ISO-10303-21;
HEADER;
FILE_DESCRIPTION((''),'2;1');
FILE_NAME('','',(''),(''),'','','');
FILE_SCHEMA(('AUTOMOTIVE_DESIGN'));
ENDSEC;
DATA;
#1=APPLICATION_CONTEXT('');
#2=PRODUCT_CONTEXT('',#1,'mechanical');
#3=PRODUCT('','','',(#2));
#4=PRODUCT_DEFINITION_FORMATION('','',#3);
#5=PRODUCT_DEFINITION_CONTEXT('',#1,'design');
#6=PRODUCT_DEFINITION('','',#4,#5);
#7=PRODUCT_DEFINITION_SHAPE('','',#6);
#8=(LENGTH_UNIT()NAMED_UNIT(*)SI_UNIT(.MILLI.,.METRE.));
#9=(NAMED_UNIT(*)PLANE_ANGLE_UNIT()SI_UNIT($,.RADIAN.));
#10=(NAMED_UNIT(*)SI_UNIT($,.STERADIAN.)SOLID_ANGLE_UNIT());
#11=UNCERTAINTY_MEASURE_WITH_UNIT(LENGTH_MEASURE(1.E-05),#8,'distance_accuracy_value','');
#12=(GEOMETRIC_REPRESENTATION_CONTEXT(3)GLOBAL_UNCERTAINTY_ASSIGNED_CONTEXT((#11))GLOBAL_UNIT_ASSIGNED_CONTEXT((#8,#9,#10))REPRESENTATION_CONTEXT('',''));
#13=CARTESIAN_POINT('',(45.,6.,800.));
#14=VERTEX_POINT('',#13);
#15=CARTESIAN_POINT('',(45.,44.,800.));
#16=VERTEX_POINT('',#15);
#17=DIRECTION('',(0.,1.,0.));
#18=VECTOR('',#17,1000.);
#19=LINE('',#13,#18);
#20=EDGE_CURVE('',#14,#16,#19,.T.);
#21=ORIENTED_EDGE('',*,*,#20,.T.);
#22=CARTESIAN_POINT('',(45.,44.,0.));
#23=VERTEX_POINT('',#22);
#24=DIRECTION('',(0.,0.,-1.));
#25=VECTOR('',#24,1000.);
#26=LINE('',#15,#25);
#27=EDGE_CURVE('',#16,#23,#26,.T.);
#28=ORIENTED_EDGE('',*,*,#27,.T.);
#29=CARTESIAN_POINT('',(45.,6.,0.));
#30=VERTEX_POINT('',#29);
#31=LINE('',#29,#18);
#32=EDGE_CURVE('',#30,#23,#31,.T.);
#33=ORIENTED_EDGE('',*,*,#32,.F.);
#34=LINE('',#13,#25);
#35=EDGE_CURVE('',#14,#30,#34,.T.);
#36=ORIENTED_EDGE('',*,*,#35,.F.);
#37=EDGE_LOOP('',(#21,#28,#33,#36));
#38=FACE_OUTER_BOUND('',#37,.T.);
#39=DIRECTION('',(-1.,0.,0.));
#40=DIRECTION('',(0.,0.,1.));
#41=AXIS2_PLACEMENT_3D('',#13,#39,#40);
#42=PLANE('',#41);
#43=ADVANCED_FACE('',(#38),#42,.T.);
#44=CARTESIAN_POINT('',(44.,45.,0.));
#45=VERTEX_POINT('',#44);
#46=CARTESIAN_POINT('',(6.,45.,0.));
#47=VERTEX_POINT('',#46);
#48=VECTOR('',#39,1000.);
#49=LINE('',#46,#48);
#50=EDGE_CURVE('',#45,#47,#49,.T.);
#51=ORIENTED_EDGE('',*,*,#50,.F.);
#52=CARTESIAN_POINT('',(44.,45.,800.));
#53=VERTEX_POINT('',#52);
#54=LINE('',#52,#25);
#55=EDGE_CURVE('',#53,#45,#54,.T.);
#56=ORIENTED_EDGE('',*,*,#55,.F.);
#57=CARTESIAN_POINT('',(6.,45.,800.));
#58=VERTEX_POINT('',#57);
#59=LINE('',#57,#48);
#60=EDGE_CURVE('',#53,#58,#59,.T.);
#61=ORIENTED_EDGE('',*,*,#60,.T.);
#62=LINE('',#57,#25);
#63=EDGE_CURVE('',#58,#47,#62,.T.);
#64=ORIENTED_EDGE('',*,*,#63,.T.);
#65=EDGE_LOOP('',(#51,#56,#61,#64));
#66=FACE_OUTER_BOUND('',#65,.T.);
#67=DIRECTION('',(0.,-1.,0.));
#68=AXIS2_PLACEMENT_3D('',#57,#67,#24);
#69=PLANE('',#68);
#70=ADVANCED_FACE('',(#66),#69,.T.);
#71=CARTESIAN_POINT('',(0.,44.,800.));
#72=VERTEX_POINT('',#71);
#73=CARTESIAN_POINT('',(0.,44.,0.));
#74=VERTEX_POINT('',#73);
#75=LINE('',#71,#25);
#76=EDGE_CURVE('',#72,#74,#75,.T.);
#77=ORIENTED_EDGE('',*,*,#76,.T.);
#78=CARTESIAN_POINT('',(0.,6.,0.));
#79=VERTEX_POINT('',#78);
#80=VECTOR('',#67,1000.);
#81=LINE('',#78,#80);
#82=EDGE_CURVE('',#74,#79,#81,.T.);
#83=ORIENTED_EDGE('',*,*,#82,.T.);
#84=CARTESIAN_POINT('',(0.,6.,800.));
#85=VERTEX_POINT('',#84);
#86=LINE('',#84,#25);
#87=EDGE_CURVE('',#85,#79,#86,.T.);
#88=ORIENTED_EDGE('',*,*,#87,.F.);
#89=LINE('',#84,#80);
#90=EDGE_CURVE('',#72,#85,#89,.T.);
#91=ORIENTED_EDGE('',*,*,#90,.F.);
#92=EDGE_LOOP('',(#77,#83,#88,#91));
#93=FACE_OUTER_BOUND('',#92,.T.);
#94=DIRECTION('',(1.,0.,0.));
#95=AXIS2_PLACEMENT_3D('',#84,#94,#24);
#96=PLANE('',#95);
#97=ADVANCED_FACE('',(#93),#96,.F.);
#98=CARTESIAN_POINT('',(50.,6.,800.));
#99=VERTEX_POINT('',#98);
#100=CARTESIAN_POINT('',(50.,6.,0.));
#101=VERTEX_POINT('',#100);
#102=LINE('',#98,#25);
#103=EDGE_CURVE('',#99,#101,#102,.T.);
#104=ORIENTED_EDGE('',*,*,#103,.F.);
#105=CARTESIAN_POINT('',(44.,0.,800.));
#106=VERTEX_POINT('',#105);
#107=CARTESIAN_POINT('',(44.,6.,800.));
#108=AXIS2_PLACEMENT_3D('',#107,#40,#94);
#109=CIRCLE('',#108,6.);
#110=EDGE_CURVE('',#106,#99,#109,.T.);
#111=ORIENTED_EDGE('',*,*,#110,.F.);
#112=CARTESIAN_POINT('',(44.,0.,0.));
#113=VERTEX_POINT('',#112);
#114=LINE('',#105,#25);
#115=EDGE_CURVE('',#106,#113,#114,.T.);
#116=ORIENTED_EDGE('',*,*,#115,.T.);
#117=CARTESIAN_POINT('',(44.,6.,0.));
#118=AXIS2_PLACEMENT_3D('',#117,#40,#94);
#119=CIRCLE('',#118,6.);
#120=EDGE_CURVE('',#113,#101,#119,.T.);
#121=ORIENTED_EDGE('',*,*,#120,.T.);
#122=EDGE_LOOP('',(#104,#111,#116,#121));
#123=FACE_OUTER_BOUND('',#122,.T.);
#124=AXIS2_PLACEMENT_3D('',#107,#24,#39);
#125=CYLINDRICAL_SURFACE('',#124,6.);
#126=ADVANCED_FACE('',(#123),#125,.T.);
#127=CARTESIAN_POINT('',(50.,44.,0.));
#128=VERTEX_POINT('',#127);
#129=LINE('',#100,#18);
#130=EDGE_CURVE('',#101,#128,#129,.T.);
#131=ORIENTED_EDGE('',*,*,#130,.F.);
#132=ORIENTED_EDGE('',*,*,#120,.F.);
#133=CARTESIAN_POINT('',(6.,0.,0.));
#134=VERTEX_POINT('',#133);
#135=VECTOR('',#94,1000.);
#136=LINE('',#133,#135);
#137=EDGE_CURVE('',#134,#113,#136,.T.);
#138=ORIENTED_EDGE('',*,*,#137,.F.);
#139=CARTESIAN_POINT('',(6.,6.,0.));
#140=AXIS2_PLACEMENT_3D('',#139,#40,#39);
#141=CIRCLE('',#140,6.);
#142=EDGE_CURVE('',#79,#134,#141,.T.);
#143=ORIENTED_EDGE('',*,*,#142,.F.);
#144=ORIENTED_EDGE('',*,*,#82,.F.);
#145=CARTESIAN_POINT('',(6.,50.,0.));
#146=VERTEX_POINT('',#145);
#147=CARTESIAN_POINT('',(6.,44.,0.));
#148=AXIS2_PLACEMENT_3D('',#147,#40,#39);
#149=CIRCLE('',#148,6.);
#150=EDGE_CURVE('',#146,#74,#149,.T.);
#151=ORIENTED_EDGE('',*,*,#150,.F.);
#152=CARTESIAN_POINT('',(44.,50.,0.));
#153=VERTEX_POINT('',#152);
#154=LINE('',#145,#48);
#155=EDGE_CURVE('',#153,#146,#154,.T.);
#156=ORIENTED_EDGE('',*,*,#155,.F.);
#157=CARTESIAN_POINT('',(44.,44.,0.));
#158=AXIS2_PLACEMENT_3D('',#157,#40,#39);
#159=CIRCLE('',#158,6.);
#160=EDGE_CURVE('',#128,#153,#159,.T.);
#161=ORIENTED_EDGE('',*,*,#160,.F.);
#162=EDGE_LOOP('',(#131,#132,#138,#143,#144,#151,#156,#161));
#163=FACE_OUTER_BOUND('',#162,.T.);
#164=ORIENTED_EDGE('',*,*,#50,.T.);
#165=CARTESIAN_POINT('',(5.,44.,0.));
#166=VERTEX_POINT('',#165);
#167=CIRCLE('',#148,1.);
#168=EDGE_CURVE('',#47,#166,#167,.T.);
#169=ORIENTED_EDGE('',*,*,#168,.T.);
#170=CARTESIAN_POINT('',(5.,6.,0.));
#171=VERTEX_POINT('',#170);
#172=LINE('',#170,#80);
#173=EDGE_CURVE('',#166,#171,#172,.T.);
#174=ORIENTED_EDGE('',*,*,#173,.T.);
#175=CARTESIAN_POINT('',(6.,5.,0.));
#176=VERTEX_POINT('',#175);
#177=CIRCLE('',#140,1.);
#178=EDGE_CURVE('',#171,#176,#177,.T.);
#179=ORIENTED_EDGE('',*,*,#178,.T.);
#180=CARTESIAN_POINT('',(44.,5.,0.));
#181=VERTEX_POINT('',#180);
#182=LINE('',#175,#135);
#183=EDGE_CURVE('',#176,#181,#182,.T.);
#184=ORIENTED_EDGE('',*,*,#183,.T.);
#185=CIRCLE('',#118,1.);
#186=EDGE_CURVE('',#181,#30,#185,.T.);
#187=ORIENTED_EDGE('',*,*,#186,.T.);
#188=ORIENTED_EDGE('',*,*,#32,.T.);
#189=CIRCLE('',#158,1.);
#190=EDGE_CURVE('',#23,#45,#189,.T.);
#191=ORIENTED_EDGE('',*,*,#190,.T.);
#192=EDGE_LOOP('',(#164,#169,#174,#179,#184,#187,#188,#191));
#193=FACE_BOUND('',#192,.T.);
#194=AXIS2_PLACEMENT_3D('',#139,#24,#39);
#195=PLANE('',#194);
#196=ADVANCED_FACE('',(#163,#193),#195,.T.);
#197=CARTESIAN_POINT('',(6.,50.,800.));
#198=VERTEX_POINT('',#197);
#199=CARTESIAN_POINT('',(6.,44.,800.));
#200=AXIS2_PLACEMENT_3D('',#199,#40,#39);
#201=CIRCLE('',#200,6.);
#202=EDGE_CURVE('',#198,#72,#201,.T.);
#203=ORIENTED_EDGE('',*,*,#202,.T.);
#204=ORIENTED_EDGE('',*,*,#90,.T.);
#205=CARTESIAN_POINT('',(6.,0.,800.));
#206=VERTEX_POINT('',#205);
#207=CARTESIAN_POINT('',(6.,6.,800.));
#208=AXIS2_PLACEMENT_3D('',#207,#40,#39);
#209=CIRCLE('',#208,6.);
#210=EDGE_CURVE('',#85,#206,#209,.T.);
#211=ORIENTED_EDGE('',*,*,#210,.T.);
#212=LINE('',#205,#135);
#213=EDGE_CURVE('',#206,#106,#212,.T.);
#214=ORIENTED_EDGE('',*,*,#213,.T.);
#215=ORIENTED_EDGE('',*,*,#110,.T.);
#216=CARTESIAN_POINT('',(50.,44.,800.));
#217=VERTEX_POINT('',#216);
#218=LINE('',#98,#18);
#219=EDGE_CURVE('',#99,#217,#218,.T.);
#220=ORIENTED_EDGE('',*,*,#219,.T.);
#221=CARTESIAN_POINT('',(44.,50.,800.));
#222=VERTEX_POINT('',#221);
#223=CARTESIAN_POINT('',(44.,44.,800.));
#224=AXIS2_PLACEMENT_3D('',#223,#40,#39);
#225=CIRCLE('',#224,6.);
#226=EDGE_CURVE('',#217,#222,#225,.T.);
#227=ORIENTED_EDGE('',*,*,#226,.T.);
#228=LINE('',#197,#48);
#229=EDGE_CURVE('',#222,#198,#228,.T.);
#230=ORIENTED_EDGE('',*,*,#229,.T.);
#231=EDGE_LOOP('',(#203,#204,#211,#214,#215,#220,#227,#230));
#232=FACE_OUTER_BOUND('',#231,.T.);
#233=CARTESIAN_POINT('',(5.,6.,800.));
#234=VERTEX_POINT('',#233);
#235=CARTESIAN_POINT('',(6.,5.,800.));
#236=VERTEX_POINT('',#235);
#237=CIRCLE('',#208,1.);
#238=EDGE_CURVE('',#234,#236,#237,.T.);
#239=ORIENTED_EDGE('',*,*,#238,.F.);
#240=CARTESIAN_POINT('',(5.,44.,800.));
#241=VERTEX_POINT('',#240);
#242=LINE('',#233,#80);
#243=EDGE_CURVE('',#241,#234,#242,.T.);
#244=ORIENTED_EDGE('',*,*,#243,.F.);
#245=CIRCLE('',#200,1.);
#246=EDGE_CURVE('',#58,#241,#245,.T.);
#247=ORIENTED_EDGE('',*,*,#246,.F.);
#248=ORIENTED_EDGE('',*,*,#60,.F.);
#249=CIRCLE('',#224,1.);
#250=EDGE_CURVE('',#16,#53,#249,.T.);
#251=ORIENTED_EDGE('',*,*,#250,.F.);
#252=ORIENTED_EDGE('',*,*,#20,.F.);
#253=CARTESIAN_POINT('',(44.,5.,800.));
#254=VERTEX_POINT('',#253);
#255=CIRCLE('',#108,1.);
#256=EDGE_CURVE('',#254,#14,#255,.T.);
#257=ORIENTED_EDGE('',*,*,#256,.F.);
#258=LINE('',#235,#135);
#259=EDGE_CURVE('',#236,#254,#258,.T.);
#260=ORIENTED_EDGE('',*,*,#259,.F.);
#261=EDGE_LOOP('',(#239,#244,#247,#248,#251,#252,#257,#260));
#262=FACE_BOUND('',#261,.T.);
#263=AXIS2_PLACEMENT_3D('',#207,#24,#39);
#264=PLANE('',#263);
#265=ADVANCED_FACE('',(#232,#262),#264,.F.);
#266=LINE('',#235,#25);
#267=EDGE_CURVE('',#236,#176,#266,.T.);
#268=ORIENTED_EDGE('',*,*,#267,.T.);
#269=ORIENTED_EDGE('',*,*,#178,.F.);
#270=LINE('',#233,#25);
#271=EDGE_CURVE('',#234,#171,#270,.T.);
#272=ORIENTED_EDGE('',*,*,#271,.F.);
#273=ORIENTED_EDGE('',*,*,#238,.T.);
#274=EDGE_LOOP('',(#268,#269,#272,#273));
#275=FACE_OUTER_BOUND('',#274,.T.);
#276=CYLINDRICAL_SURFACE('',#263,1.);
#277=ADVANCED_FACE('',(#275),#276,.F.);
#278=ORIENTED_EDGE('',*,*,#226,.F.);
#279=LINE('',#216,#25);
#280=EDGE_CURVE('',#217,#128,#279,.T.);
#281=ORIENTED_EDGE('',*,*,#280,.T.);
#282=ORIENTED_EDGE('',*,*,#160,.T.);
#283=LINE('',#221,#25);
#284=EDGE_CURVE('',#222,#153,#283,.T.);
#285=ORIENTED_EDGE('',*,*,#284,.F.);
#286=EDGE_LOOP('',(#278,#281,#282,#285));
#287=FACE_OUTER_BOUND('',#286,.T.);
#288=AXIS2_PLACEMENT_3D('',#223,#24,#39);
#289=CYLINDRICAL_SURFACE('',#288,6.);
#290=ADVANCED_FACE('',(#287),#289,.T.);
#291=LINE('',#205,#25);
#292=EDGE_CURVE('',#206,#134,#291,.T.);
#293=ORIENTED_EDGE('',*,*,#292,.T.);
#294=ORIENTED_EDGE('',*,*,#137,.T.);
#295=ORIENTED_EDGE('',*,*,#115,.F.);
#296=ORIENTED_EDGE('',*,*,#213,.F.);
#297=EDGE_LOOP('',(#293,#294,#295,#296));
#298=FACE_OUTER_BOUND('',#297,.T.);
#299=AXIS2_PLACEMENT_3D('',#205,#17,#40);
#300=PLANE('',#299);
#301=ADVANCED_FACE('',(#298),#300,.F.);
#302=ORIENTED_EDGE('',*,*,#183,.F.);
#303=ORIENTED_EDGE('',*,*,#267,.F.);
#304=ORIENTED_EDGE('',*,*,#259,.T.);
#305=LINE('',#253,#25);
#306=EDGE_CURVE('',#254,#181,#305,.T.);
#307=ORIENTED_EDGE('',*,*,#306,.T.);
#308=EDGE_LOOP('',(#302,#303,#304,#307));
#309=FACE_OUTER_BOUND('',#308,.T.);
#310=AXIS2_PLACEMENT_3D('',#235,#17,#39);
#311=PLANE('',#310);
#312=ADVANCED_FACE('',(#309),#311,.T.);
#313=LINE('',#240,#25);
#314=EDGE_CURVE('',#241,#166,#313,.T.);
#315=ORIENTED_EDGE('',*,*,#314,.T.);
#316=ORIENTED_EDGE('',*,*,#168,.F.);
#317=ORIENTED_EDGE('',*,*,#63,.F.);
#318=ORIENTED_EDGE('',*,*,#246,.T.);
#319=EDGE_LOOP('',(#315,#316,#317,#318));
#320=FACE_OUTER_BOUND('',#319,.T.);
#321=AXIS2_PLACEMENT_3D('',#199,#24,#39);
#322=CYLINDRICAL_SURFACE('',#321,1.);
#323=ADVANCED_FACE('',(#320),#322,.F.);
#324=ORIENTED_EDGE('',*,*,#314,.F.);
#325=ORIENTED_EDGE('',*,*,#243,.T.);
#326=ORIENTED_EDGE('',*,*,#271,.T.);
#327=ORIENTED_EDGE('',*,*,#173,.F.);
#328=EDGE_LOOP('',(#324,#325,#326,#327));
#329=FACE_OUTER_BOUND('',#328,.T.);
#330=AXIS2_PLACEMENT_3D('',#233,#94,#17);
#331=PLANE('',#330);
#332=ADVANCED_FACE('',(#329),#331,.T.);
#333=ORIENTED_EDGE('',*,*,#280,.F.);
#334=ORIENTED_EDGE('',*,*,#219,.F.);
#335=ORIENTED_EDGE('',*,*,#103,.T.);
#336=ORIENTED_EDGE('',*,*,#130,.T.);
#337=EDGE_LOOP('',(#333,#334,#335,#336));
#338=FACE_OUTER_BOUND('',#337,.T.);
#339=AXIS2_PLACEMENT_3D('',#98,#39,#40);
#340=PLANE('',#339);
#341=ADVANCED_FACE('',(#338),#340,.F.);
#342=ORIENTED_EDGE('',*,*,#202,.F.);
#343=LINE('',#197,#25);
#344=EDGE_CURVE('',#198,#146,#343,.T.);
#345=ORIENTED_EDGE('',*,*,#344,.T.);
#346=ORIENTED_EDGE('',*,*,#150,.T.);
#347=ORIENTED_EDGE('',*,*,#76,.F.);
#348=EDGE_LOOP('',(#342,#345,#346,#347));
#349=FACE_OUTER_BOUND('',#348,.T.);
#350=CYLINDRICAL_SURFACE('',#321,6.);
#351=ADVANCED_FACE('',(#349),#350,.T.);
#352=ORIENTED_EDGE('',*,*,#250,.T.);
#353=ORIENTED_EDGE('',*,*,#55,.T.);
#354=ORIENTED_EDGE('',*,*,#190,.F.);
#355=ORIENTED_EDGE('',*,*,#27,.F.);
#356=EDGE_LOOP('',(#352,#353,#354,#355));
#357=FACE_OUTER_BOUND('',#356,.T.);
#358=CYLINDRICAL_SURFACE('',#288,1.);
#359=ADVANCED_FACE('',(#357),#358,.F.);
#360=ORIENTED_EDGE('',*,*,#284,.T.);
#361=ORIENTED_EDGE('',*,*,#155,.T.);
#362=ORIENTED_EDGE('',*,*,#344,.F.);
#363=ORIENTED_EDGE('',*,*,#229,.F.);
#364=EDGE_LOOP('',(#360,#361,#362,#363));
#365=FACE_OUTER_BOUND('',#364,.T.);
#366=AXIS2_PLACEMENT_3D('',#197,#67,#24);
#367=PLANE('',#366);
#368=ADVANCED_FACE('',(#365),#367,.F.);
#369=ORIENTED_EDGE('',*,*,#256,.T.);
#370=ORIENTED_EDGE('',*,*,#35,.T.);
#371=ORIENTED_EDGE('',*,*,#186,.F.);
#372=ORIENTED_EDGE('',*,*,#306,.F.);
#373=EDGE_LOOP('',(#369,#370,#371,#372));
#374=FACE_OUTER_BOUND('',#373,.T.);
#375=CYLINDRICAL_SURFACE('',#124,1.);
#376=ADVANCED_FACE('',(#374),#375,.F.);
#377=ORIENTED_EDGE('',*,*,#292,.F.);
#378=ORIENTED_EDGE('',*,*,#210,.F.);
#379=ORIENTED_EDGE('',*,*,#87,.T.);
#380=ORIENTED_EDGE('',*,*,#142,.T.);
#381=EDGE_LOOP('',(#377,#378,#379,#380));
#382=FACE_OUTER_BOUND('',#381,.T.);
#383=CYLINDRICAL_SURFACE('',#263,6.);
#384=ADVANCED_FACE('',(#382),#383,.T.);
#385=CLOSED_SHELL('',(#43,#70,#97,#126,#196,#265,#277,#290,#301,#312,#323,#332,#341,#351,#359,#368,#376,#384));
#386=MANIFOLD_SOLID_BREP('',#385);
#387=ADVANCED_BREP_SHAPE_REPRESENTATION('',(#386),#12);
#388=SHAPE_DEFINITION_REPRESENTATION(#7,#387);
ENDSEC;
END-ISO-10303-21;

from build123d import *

# Parameters (mm, degrees)
BOSS_EXTRUDE1_DEPTH = 800


with BuildPart() as part:
    # Sketch1 → Boss-Extrude1 (new body)
    with BuildSketch(Plane.XY):
        with BuildLine():
            Line((6, 0), (44, 0))
            ThreePointArc((44, 0), (48.242640687, 1.757359313), (50, 6))
            Line((50, 6), (50, 44))
            ThreePointArc((50, 44), (48.242640687, 48.242640687), (44, 50))
            Line((44, 50), (6, 50))
            ThreePointArc((6, 50), (1.757359313, 48.242640687), (0, 44))
            Line((0, 44), (0, 6))
            ThreePointArc((0, 6), (1.757359313, 1.757359313), (6, 0))
        make_face()
        with BuildLine():
            Line((6, 45), (44, 45))
            ThreePointArc((44, 45), (44.707106781, 44.707106781), (45, 44))
            Line((45, 44), (45, 6))
            ThreePointArc((45, 6), (44.707106781, 5.292893219), (44, 5))
            Line((44, 5), (6, 5))
            ThreePointArc((6, 5), (5.292893219, 5.292893219), (5, 6))
            Line((5, 6), (5, 44))
            ThreePointArc((5, 44), (5.292893219, 44.707106781), (6, 45))
        make_face(mode=Mode.SUBTRACT)
    extrude(amount=BOSS_EXTRUDE1_DEPTH)


solid = part.part
